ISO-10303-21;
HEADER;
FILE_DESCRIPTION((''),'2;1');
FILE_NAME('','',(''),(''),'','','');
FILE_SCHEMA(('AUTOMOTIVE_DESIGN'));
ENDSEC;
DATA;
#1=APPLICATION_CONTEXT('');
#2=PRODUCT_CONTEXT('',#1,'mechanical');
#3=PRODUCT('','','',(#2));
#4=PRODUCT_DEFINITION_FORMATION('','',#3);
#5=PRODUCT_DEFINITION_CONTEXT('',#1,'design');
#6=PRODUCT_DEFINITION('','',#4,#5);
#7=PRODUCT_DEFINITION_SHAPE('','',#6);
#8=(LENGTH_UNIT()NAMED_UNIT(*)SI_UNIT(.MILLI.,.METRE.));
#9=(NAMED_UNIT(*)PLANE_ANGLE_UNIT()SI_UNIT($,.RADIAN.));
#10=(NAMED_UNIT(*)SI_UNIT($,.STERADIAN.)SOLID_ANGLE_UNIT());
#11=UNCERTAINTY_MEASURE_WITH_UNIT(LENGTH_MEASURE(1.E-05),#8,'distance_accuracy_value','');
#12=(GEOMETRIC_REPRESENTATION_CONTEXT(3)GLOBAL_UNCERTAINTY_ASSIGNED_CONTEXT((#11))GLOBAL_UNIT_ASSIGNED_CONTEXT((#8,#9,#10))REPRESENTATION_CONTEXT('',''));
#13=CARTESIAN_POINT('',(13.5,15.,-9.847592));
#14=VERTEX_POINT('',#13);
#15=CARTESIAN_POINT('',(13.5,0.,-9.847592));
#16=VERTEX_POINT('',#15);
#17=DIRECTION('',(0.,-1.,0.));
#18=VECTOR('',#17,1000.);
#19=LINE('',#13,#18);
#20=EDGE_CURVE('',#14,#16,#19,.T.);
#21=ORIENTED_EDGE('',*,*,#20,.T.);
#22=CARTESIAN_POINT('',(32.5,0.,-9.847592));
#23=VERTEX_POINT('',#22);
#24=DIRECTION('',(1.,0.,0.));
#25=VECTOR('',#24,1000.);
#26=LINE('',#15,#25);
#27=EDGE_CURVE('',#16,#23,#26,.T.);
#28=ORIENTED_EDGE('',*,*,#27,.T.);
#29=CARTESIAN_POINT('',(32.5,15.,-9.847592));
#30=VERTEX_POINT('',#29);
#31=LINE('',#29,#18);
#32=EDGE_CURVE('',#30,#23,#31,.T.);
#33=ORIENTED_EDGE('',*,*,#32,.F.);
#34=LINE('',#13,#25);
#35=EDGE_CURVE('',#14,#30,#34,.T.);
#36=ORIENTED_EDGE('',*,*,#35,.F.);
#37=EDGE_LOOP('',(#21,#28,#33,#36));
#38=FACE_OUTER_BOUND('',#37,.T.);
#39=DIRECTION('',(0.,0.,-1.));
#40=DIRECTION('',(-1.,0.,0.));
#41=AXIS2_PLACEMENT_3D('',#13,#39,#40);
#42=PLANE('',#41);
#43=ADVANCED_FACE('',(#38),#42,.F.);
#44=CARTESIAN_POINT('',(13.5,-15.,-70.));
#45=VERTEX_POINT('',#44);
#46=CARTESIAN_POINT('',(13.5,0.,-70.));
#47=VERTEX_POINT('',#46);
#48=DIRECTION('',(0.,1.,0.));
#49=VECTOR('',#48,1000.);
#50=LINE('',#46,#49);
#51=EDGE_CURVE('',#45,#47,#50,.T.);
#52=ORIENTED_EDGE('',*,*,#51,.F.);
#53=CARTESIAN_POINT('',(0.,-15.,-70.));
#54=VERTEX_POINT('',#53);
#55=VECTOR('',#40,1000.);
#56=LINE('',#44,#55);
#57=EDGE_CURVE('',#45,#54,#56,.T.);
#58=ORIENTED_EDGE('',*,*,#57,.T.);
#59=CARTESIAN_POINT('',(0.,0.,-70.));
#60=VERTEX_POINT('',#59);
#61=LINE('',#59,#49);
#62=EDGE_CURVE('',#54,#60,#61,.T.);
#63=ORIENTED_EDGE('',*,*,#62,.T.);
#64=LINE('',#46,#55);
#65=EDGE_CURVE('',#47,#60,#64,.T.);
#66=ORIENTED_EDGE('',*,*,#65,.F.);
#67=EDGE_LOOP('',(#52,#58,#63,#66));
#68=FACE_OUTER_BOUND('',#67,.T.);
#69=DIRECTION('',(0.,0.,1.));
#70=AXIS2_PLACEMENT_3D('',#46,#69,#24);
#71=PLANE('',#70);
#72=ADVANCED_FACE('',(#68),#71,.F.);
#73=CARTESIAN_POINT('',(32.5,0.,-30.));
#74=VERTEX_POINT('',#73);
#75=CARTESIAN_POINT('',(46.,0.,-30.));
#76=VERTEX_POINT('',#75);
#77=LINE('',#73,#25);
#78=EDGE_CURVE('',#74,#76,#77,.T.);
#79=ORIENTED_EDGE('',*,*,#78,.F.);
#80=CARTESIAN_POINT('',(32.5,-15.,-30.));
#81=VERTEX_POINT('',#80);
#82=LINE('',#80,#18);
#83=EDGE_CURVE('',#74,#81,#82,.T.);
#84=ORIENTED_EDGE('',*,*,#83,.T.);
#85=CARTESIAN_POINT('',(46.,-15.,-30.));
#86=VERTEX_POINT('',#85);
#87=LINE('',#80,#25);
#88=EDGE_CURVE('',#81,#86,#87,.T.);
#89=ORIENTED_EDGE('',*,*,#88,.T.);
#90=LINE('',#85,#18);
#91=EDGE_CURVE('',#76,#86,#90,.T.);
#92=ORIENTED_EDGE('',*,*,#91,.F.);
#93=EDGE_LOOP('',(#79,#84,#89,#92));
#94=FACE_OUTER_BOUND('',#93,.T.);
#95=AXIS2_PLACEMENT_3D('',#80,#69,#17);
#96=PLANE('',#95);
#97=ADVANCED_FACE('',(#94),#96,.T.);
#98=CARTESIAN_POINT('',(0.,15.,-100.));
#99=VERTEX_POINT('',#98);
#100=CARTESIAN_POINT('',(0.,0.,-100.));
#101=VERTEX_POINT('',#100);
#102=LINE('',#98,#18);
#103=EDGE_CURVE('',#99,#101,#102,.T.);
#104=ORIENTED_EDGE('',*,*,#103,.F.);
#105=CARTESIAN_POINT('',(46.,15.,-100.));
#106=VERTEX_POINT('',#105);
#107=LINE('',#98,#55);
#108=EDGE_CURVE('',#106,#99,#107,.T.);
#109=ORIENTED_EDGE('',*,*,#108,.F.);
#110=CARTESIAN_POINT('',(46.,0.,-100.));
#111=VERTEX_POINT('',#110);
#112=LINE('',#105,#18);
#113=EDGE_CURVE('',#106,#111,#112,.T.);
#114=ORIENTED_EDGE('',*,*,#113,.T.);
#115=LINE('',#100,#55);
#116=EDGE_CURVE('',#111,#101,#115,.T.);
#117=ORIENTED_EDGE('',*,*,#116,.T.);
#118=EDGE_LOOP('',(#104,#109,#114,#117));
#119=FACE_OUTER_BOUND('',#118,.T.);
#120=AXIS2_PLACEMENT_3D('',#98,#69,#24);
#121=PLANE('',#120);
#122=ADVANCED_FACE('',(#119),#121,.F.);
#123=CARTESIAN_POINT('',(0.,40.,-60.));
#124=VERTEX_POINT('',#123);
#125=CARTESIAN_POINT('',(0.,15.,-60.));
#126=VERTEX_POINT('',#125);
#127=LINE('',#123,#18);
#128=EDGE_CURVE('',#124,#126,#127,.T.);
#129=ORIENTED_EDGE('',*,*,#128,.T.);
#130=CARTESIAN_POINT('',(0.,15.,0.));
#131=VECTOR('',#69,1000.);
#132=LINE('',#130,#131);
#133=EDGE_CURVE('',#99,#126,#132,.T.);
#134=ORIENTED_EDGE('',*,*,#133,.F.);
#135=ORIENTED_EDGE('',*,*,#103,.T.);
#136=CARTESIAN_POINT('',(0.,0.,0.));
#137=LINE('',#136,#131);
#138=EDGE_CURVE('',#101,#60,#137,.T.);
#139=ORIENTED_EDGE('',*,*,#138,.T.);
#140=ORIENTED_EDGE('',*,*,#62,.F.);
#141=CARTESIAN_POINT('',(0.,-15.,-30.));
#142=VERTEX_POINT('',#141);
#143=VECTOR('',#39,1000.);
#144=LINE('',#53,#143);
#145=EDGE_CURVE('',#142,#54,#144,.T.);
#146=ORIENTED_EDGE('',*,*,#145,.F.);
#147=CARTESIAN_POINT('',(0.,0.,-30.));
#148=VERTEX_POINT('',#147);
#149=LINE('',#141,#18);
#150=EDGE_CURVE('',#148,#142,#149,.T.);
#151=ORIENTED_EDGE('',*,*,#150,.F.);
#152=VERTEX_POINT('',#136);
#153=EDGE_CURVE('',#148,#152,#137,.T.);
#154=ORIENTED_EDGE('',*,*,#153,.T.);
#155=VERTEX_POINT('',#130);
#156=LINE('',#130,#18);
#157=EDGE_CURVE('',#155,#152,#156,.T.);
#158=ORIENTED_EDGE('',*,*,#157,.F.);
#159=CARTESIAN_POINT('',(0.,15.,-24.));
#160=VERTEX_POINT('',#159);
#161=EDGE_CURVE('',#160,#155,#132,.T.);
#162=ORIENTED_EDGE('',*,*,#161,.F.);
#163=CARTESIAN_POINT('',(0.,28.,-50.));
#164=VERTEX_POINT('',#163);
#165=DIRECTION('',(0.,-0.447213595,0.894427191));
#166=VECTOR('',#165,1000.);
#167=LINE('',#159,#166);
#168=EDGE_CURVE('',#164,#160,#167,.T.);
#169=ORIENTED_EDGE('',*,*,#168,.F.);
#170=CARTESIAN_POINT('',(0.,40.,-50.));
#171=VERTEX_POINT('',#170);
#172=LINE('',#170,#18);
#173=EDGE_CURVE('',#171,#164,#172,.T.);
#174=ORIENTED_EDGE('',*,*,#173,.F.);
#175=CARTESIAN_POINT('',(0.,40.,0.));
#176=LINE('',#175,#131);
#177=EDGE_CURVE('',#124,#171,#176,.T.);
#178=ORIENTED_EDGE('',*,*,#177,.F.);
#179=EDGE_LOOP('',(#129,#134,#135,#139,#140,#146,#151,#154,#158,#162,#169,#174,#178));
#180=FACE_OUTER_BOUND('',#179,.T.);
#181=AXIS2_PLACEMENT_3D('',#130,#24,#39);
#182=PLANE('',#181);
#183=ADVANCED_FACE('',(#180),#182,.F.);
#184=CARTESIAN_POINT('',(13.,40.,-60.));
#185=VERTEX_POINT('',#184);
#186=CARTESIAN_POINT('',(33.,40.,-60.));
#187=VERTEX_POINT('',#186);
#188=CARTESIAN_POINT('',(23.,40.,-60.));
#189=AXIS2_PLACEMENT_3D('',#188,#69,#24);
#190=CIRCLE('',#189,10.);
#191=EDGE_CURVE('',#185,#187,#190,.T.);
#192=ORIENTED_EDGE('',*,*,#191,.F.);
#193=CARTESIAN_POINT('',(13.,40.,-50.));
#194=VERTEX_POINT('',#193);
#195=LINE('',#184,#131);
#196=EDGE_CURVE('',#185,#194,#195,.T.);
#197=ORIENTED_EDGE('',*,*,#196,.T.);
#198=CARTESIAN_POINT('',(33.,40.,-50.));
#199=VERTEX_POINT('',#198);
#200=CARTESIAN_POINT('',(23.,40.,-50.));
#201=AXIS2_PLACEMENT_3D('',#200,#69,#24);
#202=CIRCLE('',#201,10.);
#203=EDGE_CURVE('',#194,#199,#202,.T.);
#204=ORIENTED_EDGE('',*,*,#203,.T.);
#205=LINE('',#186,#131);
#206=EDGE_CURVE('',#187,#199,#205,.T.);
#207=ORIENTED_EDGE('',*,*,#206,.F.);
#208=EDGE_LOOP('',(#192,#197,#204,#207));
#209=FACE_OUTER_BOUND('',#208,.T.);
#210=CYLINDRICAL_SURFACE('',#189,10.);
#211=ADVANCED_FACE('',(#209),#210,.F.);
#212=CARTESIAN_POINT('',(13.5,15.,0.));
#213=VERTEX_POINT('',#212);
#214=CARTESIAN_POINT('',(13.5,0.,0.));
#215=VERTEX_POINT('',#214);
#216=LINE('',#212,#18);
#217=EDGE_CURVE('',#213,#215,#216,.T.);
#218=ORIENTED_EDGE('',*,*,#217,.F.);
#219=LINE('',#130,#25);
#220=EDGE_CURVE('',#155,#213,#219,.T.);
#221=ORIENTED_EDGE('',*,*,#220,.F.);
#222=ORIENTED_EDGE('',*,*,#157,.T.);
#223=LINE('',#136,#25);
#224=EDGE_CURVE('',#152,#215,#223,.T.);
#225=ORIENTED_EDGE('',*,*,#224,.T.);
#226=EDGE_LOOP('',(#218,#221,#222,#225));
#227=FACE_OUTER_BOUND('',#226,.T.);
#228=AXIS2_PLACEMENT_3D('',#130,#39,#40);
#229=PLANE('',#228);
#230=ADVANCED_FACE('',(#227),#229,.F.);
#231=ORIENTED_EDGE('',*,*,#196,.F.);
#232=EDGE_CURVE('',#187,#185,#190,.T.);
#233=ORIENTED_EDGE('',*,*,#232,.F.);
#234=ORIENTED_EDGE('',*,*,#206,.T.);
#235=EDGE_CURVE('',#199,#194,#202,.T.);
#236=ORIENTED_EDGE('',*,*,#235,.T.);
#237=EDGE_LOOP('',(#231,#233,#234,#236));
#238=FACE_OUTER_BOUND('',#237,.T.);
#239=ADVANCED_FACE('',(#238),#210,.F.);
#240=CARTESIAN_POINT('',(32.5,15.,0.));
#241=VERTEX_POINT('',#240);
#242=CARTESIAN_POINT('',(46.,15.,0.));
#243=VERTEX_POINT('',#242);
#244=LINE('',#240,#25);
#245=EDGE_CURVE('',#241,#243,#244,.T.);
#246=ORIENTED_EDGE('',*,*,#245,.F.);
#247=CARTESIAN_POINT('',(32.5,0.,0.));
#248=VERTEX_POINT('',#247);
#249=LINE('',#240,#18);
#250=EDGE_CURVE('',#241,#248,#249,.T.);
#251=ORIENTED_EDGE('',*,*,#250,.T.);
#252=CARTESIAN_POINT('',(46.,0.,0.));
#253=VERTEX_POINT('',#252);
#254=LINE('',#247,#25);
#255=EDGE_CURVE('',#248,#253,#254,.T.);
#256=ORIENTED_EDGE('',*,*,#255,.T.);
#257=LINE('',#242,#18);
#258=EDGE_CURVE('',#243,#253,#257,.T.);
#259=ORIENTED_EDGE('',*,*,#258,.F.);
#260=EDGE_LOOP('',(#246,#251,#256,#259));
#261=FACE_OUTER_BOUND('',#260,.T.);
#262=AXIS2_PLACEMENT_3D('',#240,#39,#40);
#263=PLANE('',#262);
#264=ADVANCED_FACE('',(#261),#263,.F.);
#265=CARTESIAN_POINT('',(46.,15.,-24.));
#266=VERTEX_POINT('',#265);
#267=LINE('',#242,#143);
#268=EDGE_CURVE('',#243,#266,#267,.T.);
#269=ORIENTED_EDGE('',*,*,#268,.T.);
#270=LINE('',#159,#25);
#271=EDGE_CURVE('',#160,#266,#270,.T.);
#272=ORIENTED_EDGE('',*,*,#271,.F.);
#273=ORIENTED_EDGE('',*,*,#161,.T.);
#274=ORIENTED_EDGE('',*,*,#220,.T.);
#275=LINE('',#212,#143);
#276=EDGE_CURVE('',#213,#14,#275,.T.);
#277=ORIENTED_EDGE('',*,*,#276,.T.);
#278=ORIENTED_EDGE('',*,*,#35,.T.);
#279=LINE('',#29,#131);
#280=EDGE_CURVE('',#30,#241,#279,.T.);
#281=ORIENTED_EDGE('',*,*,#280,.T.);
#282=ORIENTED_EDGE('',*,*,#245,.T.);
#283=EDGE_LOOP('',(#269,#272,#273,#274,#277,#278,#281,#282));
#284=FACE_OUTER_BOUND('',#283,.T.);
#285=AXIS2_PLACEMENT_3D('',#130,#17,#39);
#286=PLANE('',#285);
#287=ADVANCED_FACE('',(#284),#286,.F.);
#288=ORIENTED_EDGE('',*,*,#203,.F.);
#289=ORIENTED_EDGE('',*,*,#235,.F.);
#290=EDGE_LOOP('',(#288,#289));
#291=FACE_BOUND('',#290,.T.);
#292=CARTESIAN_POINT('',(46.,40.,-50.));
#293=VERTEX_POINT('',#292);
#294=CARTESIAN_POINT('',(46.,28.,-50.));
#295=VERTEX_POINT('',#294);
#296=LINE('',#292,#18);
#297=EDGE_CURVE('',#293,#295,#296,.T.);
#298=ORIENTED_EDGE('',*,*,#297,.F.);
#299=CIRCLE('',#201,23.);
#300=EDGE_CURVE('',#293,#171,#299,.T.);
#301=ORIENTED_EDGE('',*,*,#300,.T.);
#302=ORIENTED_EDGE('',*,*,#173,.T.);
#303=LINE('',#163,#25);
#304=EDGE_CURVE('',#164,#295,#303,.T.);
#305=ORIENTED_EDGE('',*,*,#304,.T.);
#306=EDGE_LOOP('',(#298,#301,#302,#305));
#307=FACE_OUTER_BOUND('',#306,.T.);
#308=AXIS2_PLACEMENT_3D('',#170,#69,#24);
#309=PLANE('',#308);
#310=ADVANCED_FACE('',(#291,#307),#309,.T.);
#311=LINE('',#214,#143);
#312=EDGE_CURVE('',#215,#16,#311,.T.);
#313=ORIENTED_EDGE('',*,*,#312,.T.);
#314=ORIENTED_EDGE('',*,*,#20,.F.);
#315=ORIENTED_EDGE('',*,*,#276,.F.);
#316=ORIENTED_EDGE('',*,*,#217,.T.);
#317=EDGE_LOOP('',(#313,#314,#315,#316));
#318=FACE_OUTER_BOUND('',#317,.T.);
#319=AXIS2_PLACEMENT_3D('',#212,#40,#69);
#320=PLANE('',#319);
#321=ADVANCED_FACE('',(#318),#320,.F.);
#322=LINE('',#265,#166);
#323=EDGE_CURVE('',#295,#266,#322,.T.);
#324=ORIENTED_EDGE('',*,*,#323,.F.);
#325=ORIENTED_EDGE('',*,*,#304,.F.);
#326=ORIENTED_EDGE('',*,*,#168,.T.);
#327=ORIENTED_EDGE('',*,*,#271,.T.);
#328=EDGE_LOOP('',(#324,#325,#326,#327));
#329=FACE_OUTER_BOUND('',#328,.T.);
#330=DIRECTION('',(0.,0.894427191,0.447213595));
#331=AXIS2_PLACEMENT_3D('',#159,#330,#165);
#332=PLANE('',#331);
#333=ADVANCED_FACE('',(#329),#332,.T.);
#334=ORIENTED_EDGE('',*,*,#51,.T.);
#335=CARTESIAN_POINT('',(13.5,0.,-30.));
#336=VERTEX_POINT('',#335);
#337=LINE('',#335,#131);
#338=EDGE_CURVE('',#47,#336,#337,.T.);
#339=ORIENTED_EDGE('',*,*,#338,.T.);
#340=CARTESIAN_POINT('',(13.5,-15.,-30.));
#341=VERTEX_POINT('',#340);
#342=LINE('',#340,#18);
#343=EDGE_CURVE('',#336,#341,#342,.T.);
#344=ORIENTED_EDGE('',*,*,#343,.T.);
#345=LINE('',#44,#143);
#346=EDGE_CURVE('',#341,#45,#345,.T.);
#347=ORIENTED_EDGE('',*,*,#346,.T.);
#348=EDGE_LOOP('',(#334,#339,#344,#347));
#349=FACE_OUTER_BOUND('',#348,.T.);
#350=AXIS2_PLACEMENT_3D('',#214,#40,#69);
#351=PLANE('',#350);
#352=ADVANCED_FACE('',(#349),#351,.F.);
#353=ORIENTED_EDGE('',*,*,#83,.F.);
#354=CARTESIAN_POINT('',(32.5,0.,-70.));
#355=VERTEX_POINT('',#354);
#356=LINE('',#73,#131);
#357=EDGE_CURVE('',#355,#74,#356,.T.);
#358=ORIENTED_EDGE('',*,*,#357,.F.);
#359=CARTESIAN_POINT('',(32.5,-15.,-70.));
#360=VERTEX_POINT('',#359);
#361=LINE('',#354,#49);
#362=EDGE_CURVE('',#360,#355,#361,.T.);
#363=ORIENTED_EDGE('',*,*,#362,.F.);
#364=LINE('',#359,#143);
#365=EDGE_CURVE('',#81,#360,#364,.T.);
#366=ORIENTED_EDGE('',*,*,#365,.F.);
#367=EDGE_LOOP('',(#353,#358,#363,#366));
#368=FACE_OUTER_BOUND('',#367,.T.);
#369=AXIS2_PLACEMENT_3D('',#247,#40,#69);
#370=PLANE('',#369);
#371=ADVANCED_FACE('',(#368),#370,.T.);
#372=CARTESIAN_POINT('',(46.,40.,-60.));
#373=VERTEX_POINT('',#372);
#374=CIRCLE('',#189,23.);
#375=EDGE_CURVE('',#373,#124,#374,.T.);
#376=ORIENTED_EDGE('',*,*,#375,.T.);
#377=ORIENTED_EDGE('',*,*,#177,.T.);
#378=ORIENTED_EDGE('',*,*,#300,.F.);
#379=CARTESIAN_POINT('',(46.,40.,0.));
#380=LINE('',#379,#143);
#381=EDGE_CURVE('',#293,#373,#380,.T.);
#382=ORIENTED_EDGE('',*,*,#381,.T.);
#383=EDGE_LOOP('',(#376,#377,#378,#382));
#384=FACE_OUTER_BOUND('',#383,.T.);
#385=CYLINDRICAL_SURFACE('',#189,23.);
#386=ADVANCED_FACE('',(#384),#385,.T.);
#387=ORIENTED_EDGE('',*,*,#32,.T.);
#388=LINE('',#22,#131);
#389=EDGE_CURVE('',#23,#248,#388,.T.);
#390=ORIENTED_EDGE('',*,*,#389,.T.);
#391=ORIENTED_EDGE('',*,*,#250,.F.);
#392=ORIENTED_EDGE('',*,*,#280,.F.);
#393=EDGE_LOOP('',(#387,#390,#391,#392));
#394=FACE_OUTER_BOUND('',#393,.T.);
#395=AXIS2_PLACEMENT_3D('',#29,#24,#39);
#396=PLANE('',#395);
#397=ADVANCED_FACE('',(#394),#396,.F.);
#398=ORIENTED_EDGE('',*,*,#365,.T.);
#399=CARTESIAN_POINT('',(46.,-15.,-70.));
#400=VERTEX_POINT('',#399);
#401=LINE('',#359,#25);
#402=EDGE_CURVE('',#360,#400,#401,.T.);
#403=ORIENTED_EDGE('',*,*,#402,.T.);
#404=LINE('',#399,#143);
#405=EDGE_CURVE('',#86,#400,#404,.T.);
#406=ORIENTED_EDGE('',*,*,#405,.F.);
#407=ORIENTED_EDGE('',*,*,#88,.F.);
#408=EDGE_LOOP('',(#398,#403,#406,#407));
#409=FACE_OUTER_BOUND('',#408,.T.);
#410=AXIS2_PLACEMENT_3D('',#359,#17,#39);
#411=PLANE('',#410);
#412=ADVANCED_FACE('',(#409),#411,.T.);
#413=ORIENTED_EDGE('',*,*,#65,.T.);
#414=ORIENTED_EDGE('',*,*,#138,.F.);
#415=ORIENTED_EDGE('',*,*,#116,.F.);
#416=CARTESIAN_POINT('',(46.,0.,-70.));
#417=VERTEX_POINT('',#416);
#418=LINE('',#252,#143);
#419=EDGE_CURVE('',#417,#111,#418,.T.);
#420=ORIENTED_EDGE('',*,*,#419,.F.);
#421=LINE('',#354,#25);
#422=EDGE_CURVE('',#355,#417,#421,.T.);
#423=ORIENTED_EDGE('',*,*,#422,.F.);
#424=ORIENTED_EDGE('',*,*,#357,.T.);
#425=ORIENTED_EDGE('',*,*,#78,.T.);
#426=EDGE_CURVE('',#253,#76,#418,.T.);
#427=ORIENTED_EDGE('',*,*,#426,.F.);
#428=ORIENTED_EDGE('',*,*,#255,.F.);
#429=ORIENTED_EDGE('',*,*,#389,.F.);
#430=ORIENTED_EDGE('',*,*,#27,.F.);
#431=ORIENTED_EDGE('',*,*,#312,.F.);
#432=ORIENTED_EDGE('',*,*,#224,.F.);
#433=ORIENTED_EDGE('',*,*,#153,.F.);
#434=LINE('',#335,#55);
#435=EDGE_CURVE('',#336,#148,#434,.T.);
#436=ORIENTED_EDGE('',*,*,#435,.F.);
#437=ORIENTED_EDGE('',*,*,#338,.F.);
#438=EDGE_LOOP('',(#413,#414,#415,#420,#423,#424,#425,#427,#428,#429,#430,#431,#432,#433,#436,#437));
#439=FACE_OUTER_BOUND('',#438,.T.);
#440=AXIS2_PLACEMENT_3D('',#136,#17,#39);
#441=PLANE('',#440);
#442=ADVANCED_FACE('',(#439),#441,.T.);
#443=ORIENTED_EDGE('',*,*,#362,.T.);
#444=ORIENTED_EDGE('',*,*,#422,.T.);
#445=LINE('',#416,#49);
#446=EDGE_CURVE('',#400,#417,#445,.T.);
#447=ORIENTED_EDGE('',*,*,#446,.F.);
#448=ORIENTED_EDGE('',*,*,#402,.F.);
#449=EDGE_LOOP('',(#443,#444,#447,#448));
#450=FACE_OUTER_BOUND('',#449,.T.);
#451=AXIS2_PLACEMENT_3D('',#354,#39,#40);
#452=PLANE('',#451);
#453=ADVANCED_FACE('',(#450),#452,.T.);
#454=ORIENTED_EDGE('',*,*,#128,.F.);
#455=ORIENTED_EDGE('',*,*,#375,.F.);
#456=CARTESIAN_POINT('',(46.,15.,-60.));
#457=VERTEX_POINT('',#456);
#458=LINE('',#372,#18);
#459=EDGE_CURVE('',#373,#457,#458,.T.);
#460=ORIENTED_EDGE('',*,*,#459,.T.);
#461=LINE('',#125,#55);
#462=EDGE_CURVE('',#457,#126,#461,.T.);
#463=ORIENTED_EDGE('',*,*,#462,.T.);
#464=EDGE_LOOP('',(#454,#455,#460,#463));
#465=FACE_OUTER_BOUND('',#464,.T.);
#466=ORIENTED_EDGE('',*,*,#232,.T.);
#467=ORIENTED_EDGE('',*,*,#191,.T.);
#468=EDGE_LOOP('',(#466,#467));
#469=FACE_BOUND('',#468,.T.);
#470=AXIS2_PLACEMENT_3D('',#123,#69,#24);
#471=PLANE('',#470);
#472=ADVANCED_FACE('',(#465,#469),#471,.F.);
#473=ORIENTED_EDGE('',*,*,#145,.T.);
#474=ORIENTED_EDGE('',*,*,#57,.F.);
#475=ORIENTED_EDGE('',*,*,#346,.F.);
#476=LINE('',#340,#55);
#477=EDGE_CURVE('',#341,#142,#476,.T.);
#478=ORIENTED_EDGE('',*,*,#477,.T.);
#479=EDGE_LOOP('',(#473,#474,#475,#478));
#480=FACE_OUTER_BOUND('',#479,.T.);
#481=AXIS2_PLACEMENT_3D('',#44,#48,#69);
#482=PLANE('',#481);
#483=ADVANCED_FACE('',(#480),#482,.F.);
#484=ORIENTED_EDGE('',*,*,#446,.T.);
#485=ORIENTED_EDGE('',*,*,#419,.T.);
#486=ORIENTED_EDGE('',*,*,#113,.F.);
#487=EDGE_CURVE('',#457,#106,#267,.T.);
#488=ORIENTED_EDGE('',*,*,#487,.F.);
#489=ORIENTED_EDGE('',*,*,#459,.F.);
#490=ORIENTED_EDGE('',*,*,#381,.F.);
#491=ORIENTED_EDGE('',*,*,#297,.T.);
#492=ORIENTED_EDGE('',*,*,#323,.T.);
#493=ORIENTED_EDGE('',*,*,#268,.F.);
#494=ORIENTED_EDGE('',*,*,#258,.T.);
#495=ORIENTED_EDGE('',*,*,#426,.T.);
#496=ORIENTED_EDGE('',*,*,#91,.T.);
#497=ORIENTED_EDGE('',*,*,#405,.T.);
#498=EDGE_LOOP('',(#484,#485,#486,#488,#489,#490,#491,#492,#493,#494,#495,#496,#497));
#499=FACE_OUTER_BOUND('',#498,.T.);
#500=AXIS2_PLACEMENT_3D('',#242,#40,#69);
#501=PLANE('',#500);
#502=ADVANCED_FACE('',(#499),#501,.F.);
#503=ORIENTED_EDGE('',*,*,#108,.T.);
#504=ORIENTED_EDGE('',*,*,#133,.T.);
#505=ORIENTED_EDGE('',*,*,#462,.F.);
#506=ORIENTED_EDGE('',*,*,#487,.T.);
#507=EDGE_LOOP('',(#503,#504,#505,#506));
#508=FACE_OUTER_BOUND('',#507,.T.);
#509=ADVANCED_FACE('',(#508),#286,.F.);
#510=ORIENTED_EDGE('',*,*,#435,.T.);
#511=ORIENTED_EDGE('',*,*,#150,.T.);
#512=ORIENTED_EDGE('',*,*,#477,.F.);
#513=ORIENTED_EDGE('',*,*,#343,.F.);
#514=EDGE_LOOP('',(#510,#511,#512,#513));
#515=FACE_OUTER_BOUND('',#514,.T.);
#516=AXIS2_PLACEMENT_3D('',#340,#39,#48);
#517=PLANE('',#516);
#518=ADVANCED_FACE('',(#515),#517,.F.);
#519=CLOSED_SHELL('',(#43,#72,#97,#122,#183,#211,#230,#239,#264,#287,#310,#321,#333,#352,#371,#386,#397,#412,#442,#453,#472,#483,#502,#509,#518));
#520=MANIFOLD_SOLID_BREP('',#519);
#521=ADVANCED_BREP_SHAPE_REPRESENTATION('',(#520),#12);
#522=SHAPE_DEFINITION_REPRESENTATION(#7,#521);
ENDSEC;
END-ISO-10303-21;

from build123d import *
from build123d.topology import SkipClean

# Parameters (mm, degrees)
BASE_PLATE_DEPTH      = 15
SIDE_BLOCK_A_SKETCH_W = 40
SIDE_BLOCK_A_SKETCH_H = 15
SIDE_BLOCK_A_DEPTH    = 13.5
SIDE_BLOCK_B_SKETCH_W = 40
SIDE_BLOCK_B_SKETCH_H = 15
SIDE_BLOCK_B_DEPTH    = 13.5
UPRIGHT_WEB_SKETCH_W  = 46
UPRIGHT_WEB_SKETCH_H  = 10
UPRIGHT_WEB_DEPTH     = 25
LUG_EAR_DEPTH         = 10
LUG_HOLE_SKETCH_R     = 10
LUG_HOLE_DEPTH        = 10
GUSSET_DEPTH          = 46


with BuildPart() as part:
    # Base Plate Sketch → Base Plate (new body)
    with BuildSketch(Plane(origin=(0, 0, 0), x_dir=(1, 0, 0), z_dir=(0, 1, 0))):
        Polygon((13.5, 0), (13.5, 9.84759163), (32.5, 9.84759163), (32.5, 0), (46, 0), (46, 100), (0, 100), (0, 0), align=None)
    extrude(amount=BASE_PLATE_DEPTH)

    # Side Block A Sketch → Side Block A (add)
    with BuildSketch(Plane(origin=(0, 0, 0), x_dir=(0, 0, -1), z_dir=(1, 0, 0))):
        with Locations((50, -7.5)):
            Rectangle(SIDE_BLOCK_A_SKETCH_W, SIDE_BLOCK_A_SKETCH_H)
    extrude(amount=SIDE_BLOCK_A_DEPTH)

    # Side Block B Sketch → Side Block B (add)
    with BuildSketch(Plane(origin=(46, 0, 0), x_dir=(0, 0, -1), z_dir=(1, 0, 0))):
        with Locations((50, -7.5)):
            Rectangle(SIDE_BLOCK_B_SKETCH_W, SIDE_BLOCK_B_SKETCH_H)
    extrude(amount=-SIDE_BLOCK_B_DEPTH)

    # Upright Web Sketch → Upright Web (add)
    with BuildSketch(Plane(origin=(0, 15, 0), x_dir=(1, 0, 0), z_dir=(0, 1, 0))):
        with Locations((23, 55)):
            Rectangle(UPRIGHT_WEB_SKETCH_W, UPRIGHT_WEB_SKETCH_H)
    extrude(amount=UPRIGHT_WEB_DEPTH)

    # Lug Ear Sketch → Lug Ear (add)
    with BuildSketch(Plane.XY.offset(-50)):
        with BuildLine():
            ThreePointArc((33, 40), (23, 30), (13, 40))
            Line((13, 40), (0, 40))
            ThreePointArc((0, 40), (23, 17), (46, 40))
            Line((46, 40), (33, 40))
        make_face()
        with BuildLine():
            Line((0, 40), (13, 40))
            ThreePointArc((13, 40), (23, 50), (33, 40))
            Line((33, 40), (46, 40))
            ThreePointArc((46, 40), (23, 63), (0, 40))
        make_face()
    extrude(amount=-LUG_EAR_DEPTH)

    # Lug Hole Sketch → Lug Hole (cut)
    with SkipClean():  # the faces are left unmerged after this step: merging them gives an invalid solid
        with BuildSketch(Plane.XY.offset(-50)):
            with Locations((23, 40)):
                Circle(LUG_HOLE_SKETCH_R)
        extrude(amount=-LUG_HOLE_DEPTH, mode=Mode.SUBTRACT)

    # Gusset Sketch → Gusset (add)
    with SkipClean():  # the faces are left unmerged after this step: merging them gives an invalid solid
        with BuildSketch(Plane(origin=(46, 0, 0), x_dir=(0, 0, -1), z_dir=(1, 0, 0))):
            Polygon((50, 15), (24, 15), (50, 28), align=None)
        extrude(amount=-GUSSET_DEPTH)


solid = part.part
